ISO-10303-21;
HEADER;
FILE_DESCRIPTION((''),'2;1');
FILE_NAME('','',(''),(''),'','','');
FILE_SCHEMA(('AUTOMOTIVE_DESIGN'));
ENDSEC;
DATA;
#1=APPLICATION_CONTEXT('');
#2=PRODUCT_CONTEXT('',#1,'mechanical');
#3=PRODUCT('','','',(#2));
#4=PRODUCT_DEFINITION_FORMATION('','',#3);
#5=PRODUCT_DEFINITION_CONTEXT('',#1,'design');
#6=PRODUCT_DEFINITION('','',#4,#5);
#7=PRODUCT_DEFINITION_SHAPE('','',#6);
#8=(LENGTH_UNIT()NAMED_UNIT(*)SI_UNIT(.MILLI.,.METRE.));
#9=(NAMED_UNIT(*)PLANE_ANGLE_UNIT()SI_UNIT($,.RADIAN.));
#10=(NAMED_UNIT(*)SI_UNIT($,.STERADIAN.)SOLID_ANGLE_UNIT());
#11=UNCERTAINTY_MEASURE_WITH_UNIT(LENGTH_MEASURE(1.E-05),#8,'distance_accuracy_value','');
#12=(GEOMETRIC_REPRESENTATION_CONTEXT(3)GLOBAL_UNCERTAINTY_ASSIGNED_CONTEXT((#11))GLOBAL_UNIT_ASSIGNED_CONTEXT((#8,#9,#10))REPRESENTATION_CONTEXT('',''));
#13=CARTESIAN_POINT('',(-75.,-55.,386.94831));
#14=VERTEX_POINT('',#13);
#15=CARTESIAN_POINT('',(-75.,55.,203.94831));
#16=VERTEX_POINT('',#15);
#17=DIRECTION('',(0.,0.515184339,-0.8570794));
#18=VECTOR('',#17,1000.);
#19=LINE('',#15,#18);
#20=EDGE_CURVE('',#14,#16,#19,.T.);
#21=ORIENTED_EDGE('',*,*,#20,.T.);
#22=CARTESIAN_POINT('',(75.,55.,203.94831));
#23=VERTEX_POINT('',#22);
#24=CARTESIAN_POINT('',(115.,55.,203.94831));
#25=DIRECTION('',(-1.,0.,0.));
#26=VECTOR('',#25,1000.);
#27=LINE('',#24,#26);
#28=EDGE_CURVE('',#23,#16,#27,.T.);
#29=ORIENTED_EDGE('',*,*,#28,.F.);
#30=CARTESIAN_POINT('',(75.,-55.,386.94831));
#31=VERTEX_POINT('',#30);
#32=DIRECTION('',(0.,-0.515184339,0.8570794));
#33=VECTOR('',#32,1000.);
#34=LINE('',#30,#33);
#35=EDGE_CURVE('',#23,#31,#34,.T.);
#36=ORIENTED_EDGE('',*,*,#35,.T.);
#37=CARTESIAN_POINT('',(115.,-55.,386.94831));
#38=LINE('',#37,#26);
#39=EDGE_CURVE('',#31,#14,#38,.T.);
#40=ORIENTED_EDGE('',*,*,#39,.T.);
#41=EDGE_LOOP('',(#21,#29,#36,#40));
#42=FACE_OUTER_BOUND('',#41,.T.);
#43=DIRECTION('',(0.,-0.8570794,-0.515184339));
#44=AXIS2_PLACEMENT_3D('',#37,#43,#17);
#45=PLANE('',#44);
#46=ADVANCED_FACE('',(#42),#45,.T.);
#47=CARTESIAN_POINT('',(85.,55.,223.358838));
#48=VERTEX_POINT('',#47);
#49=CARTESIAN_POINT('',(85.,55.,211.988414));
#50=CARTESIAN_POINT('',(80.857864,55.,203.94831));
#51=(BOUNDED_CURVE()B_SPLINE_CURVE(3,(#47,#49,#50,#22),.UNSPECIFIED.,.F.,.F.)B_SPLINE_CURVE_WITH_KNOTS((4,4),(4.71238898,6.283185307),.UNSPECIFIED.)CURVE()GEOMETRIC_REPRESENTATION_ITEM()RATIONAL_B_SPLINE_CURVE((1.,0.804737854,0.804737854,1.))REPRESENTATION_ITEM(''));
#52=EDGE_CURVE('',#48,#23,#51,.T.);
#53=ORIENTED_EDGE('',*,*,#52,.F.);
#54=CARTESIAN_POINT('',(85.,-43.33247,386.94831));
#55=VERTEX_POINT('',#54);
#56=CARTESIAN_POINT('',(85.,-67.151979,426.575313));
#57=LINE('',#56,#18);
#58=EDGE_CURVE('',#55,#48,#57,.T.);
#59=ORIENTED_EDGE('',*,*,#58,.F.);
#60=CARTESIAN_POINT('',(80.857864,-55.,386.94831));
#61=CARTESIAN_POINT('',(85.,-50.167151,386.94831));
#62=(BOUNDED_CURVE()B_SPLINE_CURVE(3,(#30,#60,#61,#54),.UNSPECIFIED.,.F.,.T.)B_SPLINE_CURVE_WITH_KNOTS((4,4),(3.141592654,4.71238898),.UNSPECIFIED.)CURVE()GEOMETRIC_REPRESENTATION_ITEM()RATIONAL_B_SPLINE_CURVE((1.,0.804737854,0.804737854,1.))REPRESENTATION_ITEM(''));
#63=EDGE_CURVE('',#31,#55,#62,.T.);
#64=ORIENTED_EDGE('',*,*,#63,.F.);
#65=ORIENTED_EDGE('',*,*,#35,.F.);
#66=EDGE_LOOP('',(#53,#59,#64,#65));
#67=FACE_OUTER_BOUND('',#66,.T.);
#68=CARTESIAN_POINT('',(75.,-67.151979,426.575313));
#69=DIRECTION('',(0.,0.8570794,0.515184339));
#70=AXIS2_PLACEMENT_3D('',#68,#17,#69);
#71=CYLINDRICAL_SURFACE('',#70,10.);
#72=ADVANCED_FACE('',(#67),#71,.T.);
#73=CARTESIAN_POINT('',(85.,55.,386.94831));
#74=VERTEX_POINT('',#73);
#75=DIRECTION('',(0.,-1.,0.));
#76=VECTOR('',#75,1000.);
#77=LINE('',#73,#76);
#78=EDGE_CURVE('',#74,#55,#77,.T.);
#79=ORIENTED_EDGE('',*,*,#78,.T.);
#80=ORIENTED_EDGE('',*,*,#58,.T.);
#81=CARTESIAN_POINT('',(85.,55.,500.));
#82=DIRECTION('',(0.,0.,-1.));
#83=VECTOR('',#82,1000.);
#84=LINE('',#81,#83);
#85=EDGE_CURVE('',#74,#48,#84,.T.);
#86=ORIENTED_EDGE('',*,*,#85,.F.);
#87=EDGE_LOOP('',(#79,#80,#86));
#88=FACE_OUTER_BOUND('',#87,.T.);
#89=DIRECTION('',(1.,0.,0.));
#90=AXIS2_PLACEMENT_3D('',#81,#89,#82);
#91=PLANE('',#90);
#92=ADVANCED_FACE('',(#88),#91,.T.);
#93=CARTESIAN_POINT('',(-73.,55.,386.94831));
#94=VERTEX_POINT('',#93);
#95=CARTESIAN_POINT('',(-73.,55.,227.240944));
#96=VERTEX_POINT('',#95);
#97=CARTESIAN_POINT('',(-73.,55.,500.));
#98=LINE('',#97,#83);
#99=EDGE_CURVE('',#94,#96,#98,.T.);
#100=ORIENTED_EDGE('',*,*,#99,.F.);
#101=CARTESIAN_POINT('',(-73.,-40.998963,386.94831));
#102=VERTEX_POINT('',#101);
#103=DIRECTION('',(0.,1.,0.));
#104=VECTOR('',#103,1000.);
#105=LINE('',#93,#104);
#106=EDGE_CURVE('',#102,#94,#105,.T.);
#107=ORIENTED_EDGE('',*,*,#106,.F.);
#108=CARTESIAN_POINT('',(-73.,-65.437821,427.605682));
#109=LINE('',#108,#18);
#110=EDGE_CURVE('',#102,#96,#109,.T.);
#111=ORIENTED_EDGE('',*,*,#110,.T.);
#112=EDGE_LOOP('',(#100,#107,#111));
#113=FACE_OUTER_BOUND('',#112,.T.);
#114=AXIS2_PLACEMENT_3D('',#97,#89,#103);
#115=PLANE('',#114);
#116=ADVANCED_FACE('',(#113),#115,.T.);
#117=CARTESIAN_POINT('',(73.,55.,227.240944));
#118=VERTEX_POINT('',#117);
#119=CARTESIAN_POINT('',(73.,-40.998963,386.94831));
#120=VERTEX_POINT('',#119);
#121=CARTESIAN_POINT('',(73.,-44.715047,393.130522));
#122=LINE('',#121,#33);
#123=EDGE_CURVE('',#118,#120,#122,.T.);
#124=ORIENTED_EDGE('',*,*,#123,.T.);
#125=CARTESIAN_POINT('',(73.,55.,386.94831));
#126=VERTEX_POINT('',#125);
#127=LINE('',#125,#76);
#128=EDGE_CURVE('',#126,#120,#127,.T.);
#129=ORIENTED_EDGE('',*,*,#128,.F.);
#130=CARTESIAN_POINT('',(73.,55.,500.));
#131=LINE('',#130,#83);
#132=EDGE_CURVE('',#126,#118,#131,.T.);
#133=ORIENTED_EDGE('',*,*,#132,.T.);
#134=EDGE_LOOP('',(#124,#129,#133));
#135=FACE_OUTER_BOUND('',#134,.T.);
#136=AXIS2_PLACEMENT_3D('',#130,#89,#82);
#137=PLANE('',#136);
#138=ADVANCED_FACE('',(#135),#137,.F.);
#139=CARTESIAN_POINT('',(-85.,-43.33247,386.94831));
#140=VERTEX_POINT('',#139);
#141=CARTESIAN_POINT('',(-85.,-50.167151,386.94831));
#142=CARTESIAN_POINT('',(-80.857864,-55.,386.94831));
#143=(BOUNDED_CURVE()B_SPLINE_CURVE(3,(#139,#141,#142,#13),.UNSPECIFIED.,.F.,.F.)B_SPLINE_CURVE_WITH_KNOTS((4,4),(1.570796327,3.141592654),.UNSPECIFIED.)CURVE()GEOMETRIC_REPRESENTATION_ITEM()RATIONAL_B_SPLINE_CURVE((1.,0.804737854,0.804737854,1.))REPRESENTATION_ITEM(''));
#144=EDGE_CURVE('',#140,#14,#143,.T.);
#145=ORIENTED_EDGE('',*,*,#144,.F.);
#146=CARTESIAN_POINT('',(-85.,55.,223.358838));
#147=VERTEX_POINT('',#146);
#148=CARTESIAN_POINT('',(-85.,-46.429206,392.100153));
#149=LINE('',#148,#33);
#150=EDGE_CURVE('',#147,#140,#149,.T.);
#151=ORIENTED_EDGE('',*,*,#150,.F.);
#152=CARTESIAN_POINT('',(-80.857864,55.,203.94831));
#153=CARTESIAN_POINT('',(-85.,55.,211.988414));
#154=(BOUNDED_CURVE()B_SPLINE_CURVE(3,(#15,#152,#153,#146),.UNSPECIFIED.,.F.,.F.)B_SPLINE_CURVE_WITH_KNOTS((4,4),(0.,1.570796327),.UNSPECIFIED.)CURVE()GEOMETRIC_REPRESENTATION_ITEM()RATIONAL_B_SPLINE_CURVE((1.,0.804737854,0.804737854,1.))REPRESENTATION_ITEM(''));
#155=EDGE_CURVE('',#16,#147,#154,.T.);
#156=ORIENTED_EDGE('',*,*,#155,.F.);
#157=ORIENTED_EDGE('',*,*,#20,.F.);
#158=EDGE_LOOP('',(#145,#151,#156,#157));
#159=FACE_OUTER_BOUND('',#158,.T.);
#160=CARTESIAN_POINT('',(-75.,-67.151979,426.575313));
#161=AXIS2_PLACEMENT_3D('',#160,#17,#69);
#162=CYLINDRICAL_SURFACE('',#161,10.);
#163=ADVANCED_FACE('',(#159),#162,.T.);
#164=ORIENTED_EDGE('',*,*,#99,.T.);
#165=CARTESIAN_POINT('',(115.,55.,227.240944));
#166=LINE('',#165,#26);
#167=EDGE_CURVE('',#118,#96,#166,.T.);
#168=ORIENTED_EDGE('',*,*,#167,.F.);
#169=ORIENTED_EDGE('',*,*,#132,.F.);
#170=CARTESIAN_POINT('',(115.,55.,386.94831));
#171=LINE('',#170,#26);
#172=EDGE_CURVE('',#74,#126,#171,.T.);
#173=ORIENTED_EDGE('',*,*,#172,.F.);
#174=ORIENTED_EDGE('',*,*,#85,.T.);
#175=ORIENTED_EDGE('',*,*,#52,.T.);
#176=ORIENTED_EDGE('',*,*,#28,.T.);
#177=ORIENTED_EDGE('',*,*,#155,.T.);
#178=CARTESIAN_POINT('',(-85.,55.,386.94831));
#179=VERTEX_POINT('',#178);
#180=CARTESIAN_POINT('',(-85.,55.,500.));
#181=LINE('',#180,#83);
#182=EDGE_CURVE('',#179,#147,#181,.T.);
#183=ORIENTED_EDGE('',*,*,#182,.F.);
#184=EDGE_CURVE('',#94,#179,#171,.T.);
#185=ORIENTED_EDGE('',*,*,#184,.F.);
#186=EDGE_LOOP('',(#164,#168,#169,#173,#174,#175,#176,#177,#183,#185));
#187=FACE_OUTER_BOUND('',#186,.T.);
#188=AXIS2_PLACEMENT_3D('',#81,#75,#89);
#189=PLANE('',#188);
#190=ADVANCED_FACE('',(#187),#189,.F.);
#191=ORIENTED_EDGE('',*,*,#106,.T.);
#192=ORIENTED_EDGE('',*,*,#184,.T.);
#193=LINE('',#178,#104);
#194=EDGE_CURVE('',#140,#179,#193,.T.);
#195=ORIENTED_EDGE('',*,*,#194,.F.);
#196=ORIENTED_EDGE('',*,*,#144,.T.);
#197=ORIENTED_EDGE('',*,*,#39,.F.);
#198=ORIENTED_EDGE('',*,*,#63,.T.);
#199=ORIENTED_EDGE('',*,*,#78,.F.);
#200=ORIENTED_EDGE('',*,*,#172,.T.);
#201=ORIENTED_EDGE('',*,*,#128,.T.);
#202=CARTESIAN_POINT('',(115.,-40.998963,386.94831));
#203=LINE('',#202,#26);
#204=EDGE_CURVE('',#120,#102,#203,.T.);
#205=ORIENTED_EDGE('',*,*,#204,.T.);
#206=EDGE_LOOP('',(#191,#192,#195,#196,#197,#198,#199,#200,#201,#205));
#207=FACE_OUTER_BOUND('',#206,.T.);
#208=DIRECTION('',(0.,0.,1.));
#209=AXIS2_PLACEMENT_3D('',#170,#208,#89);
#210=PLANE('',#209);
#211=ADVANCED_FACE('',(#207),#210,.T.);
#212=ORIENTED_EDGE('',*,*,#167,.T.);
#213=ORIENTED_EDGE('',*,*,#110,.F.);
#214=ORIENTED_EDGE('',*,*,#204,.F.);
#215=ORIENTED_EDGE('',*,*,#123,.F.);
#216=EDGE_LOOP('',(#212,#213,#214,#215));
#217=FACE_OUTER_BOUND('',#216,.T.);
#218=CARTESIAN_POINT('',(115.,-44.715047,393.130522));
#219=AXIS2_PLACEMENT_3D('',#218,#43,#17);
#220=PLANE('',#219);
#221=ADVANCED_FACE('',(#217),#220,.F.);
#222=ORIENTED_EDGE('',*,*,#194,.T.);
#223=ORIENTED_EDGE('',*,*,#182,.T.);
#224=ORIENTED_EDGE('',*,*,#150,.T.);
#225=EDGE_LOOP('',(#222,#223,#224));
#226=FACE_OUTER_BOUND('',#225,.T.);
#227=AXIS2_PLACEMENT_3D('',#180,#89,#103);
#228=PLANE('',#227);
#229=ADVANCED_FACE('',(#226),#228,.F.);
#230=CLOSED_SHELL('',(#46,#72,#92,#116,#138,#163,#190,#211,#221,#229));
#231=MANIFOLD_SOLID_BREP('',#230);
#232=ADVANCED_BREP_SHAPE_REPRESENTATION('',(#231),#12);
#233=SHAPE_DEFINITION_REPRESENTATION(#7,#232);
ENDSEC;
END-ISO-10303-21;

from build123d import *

# Parameters (mm, degrees)
SKETCH_2_W          = 170
SKETCH_2_H          = 110
EXTRUDE_2_DEPTH     = 500
SKETCH_5_OUTSIDE_W  = 609.888
SKETCH_5_OUTSIDE_H  = 219.888
CUT_EXTRUDE_3_DEPTH = 200
FILLET_2_R          = 10
SHELL_2_T           = -12


with BuildPart() as part:
    # 草图2 → 凸台-拉伸2 (new body)
    with BuildSketch(Plane.XY):
        Rectangle(SKETCH_2_W, SKETCH_2_H)
    extrude(amount=EXTRUDE_2_DEPTH)

    # 草图5 outside → 切除-拉伸3 (cut)
    with BuildSketch(Plane.ZY.offset(85)):
        with Locations((250, 0)):
            Rectangle(SKETCH_5_OUTSIDE_W, SKETCH_5_OUTSIDE_H)
        Polygon((386.948309985, 55), (386.948309985, -55), (203.948309985, 55), align=None, mode=Mode.SUBTRACT)
    extrude(amount=-CUT_EXTRUDE_3_DEPTH, mode=Mode.SUBTRACT)

    # 圆角2
    fillet_2_edges = [part.edges().sort_by_distance(p)[0] for p in [
        (85, 0, 295.448309985),
        (-85, 0, 295.448309985),
    ]]
    fillet(fillet_2_edges, radius=FILLET_2_R)

    # 抽壳2
    shell_2_openings = [part.faces().sort_by_distance(p)[0] for p in [
        (0, 55, 295.682357503),
        (0, 0.1406843, 386.948309985),
    ]]
    offset(amount=SHELL_2_T, openings=shell_2_openings, kind=Kind.INTERSECTION)


solid = part.part
